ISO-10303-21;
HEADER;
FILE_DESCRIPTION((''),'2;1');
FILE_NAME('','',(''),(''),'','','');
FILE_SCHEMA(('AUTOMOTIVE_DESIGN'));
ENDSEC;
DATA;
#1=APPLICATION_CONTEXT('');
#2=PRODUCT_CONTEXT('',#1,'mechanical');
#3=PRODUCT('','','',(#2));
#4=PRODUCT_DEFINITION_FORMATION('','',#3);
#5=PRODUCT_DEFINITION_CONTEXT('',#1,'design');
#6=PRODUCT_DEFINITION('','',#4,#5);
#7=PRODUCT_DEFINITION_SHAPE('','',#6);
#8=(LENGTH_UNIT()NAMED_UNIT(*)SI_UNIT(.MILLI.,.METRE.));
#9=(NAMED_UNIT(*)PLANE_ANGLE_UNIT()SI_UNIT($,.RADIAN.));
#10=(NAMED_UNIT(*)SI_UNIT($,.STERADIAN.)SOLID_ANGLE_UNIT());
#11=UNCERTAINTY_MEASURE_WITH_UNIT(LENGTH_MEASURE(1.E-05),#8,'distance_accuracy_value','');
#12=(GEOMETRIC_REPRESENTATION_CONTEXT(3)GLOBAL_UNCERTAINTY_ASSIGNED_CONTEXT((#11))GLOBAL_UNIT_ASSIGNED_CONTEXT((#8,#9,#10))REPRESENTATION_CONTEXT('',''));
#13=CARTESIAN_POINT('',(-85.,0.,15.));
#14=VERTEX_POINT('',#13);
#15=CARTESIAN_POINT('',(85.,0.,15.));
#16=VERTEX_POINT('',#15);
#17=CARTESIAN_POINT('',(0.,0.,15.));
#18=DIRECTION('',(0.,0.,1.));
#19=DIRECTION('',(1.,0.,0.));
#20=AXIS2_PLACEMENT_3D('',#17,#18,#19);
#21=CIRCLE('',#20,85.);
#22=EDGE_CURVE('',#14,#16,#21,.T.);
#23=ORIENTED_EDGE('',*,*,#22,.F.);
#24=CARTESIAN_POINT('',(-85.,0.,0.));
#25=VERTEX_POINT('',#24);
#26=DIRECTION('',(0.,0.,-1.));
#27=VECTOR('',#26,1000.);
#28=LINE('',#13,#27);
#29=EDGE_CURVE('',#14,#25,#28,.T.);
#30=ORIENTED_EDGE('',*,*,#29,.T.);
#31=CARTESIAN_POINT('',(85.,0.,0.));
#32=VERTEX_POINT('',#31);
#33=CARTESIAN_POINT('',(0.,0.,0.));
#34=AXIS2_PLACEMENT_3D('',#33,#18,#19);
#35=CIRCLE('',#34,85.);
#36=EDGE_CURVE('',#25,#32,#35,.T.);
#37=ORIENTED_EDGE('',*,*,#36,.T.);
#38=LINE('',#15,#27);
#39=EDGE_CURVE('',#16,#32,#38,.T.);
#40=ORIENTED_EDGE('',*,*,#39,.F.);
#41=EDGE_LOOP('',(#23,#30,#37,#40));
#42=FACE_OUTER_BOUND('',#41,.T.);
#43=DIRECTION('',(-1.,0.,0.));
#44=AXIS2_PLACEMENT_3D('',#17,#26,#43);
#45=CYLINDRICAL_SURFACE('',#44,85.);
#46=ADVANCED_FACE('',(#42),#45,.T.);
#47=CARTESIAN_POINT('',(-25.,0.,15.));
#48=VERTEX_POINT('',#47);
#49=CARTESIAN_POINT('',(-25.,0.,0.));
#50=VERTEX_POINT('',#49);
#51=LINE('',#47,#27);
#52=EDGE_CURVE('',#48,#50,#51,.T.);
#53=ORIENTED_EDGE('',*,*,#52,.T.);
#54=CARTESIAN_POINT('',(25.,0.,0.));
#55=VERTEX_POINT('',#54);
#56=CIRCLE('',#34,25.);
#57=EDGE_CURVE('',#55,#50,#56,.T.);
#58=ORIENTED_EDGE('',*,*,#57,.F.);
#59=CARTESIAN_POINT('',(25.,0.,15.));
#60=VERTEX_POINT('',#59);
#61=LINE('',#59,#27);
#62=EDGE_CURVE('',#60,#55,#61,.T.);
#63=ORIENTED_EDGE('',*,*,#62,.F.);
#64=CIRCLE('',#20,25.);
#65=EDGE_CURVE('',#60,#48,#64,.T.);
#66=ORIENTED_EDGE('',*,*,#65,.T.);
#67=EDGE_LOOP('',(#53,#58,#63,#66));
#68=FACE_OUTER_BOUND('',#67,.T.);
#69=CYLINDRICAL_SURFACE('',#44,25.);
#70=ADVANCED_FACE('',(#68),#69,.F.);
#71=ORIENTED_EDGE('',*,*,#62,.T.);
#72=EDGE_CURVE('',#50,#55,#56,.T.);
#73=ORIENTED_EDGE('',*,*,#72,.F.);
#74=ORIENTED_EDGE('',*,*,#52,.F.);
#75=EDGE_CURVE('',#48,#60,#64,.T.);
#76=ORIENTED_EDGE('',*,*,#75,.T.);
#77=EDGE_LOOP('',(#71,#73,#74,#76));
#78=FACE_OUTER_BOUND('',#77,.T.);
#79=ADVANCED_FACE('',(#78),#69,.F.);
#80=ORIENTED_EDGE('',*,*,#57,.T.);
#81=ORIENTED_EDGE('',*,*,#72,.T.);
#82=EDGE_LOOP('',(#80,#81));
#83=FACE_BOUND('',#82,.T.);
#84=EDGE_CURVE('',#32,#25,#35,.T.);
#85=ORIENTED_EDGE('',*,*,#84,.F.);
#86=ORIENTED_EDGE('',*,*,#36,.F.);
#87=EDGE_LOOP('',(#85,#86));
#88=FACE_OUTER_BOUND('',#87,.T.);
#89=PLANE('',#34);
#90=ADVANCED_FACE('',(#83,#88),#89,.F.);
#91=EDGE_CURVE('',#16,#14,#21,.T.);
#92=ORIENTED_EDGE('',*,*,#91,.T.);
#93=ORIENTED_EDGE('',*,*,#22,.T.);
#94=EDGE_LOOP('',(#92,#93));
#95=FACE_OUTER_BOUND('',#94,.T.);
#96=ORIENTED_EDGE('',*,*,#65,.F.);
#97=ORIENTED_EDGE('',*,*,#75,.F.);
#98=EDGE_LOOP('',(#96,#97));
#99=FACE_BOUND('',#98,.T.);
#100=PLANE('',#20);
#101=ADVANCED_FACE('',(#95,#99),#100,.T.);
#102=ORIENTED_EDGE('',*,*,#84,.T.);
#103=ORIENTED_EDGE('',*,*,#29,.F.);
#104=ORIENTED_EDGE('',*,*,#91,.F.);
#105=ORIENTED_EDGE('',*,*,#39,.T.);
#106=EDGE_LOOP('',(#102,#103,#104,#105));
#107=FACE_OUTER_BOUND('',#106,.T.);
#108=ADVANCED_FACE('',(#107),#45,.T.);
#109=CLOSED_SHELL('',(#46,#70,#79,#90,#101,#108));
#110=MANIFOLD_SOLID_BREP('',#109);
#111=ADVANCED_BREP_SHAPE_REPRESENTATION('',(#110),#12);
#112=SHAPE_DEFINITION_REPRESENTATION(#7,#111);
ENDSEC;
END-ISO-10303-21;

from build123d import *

# Parameters (mm, degrees)
SKETCH1_R           = 85
SKETCH1_R_2         = 25
BOSS_EXTRUDE1_DEPTH = 15


with BuildPart() as part:
    # Sketch1 → Boss-Extrude1 (new body)
    with BuildSketch(Plane.XY):
        Circle(SKETCH1_R)
        Circle(SKETCH1_R_2, mode=Mode.SUBTRACT)
    extrude(amount=BOSS_EXTRUDE1_DEPTH)


solid = part.part
